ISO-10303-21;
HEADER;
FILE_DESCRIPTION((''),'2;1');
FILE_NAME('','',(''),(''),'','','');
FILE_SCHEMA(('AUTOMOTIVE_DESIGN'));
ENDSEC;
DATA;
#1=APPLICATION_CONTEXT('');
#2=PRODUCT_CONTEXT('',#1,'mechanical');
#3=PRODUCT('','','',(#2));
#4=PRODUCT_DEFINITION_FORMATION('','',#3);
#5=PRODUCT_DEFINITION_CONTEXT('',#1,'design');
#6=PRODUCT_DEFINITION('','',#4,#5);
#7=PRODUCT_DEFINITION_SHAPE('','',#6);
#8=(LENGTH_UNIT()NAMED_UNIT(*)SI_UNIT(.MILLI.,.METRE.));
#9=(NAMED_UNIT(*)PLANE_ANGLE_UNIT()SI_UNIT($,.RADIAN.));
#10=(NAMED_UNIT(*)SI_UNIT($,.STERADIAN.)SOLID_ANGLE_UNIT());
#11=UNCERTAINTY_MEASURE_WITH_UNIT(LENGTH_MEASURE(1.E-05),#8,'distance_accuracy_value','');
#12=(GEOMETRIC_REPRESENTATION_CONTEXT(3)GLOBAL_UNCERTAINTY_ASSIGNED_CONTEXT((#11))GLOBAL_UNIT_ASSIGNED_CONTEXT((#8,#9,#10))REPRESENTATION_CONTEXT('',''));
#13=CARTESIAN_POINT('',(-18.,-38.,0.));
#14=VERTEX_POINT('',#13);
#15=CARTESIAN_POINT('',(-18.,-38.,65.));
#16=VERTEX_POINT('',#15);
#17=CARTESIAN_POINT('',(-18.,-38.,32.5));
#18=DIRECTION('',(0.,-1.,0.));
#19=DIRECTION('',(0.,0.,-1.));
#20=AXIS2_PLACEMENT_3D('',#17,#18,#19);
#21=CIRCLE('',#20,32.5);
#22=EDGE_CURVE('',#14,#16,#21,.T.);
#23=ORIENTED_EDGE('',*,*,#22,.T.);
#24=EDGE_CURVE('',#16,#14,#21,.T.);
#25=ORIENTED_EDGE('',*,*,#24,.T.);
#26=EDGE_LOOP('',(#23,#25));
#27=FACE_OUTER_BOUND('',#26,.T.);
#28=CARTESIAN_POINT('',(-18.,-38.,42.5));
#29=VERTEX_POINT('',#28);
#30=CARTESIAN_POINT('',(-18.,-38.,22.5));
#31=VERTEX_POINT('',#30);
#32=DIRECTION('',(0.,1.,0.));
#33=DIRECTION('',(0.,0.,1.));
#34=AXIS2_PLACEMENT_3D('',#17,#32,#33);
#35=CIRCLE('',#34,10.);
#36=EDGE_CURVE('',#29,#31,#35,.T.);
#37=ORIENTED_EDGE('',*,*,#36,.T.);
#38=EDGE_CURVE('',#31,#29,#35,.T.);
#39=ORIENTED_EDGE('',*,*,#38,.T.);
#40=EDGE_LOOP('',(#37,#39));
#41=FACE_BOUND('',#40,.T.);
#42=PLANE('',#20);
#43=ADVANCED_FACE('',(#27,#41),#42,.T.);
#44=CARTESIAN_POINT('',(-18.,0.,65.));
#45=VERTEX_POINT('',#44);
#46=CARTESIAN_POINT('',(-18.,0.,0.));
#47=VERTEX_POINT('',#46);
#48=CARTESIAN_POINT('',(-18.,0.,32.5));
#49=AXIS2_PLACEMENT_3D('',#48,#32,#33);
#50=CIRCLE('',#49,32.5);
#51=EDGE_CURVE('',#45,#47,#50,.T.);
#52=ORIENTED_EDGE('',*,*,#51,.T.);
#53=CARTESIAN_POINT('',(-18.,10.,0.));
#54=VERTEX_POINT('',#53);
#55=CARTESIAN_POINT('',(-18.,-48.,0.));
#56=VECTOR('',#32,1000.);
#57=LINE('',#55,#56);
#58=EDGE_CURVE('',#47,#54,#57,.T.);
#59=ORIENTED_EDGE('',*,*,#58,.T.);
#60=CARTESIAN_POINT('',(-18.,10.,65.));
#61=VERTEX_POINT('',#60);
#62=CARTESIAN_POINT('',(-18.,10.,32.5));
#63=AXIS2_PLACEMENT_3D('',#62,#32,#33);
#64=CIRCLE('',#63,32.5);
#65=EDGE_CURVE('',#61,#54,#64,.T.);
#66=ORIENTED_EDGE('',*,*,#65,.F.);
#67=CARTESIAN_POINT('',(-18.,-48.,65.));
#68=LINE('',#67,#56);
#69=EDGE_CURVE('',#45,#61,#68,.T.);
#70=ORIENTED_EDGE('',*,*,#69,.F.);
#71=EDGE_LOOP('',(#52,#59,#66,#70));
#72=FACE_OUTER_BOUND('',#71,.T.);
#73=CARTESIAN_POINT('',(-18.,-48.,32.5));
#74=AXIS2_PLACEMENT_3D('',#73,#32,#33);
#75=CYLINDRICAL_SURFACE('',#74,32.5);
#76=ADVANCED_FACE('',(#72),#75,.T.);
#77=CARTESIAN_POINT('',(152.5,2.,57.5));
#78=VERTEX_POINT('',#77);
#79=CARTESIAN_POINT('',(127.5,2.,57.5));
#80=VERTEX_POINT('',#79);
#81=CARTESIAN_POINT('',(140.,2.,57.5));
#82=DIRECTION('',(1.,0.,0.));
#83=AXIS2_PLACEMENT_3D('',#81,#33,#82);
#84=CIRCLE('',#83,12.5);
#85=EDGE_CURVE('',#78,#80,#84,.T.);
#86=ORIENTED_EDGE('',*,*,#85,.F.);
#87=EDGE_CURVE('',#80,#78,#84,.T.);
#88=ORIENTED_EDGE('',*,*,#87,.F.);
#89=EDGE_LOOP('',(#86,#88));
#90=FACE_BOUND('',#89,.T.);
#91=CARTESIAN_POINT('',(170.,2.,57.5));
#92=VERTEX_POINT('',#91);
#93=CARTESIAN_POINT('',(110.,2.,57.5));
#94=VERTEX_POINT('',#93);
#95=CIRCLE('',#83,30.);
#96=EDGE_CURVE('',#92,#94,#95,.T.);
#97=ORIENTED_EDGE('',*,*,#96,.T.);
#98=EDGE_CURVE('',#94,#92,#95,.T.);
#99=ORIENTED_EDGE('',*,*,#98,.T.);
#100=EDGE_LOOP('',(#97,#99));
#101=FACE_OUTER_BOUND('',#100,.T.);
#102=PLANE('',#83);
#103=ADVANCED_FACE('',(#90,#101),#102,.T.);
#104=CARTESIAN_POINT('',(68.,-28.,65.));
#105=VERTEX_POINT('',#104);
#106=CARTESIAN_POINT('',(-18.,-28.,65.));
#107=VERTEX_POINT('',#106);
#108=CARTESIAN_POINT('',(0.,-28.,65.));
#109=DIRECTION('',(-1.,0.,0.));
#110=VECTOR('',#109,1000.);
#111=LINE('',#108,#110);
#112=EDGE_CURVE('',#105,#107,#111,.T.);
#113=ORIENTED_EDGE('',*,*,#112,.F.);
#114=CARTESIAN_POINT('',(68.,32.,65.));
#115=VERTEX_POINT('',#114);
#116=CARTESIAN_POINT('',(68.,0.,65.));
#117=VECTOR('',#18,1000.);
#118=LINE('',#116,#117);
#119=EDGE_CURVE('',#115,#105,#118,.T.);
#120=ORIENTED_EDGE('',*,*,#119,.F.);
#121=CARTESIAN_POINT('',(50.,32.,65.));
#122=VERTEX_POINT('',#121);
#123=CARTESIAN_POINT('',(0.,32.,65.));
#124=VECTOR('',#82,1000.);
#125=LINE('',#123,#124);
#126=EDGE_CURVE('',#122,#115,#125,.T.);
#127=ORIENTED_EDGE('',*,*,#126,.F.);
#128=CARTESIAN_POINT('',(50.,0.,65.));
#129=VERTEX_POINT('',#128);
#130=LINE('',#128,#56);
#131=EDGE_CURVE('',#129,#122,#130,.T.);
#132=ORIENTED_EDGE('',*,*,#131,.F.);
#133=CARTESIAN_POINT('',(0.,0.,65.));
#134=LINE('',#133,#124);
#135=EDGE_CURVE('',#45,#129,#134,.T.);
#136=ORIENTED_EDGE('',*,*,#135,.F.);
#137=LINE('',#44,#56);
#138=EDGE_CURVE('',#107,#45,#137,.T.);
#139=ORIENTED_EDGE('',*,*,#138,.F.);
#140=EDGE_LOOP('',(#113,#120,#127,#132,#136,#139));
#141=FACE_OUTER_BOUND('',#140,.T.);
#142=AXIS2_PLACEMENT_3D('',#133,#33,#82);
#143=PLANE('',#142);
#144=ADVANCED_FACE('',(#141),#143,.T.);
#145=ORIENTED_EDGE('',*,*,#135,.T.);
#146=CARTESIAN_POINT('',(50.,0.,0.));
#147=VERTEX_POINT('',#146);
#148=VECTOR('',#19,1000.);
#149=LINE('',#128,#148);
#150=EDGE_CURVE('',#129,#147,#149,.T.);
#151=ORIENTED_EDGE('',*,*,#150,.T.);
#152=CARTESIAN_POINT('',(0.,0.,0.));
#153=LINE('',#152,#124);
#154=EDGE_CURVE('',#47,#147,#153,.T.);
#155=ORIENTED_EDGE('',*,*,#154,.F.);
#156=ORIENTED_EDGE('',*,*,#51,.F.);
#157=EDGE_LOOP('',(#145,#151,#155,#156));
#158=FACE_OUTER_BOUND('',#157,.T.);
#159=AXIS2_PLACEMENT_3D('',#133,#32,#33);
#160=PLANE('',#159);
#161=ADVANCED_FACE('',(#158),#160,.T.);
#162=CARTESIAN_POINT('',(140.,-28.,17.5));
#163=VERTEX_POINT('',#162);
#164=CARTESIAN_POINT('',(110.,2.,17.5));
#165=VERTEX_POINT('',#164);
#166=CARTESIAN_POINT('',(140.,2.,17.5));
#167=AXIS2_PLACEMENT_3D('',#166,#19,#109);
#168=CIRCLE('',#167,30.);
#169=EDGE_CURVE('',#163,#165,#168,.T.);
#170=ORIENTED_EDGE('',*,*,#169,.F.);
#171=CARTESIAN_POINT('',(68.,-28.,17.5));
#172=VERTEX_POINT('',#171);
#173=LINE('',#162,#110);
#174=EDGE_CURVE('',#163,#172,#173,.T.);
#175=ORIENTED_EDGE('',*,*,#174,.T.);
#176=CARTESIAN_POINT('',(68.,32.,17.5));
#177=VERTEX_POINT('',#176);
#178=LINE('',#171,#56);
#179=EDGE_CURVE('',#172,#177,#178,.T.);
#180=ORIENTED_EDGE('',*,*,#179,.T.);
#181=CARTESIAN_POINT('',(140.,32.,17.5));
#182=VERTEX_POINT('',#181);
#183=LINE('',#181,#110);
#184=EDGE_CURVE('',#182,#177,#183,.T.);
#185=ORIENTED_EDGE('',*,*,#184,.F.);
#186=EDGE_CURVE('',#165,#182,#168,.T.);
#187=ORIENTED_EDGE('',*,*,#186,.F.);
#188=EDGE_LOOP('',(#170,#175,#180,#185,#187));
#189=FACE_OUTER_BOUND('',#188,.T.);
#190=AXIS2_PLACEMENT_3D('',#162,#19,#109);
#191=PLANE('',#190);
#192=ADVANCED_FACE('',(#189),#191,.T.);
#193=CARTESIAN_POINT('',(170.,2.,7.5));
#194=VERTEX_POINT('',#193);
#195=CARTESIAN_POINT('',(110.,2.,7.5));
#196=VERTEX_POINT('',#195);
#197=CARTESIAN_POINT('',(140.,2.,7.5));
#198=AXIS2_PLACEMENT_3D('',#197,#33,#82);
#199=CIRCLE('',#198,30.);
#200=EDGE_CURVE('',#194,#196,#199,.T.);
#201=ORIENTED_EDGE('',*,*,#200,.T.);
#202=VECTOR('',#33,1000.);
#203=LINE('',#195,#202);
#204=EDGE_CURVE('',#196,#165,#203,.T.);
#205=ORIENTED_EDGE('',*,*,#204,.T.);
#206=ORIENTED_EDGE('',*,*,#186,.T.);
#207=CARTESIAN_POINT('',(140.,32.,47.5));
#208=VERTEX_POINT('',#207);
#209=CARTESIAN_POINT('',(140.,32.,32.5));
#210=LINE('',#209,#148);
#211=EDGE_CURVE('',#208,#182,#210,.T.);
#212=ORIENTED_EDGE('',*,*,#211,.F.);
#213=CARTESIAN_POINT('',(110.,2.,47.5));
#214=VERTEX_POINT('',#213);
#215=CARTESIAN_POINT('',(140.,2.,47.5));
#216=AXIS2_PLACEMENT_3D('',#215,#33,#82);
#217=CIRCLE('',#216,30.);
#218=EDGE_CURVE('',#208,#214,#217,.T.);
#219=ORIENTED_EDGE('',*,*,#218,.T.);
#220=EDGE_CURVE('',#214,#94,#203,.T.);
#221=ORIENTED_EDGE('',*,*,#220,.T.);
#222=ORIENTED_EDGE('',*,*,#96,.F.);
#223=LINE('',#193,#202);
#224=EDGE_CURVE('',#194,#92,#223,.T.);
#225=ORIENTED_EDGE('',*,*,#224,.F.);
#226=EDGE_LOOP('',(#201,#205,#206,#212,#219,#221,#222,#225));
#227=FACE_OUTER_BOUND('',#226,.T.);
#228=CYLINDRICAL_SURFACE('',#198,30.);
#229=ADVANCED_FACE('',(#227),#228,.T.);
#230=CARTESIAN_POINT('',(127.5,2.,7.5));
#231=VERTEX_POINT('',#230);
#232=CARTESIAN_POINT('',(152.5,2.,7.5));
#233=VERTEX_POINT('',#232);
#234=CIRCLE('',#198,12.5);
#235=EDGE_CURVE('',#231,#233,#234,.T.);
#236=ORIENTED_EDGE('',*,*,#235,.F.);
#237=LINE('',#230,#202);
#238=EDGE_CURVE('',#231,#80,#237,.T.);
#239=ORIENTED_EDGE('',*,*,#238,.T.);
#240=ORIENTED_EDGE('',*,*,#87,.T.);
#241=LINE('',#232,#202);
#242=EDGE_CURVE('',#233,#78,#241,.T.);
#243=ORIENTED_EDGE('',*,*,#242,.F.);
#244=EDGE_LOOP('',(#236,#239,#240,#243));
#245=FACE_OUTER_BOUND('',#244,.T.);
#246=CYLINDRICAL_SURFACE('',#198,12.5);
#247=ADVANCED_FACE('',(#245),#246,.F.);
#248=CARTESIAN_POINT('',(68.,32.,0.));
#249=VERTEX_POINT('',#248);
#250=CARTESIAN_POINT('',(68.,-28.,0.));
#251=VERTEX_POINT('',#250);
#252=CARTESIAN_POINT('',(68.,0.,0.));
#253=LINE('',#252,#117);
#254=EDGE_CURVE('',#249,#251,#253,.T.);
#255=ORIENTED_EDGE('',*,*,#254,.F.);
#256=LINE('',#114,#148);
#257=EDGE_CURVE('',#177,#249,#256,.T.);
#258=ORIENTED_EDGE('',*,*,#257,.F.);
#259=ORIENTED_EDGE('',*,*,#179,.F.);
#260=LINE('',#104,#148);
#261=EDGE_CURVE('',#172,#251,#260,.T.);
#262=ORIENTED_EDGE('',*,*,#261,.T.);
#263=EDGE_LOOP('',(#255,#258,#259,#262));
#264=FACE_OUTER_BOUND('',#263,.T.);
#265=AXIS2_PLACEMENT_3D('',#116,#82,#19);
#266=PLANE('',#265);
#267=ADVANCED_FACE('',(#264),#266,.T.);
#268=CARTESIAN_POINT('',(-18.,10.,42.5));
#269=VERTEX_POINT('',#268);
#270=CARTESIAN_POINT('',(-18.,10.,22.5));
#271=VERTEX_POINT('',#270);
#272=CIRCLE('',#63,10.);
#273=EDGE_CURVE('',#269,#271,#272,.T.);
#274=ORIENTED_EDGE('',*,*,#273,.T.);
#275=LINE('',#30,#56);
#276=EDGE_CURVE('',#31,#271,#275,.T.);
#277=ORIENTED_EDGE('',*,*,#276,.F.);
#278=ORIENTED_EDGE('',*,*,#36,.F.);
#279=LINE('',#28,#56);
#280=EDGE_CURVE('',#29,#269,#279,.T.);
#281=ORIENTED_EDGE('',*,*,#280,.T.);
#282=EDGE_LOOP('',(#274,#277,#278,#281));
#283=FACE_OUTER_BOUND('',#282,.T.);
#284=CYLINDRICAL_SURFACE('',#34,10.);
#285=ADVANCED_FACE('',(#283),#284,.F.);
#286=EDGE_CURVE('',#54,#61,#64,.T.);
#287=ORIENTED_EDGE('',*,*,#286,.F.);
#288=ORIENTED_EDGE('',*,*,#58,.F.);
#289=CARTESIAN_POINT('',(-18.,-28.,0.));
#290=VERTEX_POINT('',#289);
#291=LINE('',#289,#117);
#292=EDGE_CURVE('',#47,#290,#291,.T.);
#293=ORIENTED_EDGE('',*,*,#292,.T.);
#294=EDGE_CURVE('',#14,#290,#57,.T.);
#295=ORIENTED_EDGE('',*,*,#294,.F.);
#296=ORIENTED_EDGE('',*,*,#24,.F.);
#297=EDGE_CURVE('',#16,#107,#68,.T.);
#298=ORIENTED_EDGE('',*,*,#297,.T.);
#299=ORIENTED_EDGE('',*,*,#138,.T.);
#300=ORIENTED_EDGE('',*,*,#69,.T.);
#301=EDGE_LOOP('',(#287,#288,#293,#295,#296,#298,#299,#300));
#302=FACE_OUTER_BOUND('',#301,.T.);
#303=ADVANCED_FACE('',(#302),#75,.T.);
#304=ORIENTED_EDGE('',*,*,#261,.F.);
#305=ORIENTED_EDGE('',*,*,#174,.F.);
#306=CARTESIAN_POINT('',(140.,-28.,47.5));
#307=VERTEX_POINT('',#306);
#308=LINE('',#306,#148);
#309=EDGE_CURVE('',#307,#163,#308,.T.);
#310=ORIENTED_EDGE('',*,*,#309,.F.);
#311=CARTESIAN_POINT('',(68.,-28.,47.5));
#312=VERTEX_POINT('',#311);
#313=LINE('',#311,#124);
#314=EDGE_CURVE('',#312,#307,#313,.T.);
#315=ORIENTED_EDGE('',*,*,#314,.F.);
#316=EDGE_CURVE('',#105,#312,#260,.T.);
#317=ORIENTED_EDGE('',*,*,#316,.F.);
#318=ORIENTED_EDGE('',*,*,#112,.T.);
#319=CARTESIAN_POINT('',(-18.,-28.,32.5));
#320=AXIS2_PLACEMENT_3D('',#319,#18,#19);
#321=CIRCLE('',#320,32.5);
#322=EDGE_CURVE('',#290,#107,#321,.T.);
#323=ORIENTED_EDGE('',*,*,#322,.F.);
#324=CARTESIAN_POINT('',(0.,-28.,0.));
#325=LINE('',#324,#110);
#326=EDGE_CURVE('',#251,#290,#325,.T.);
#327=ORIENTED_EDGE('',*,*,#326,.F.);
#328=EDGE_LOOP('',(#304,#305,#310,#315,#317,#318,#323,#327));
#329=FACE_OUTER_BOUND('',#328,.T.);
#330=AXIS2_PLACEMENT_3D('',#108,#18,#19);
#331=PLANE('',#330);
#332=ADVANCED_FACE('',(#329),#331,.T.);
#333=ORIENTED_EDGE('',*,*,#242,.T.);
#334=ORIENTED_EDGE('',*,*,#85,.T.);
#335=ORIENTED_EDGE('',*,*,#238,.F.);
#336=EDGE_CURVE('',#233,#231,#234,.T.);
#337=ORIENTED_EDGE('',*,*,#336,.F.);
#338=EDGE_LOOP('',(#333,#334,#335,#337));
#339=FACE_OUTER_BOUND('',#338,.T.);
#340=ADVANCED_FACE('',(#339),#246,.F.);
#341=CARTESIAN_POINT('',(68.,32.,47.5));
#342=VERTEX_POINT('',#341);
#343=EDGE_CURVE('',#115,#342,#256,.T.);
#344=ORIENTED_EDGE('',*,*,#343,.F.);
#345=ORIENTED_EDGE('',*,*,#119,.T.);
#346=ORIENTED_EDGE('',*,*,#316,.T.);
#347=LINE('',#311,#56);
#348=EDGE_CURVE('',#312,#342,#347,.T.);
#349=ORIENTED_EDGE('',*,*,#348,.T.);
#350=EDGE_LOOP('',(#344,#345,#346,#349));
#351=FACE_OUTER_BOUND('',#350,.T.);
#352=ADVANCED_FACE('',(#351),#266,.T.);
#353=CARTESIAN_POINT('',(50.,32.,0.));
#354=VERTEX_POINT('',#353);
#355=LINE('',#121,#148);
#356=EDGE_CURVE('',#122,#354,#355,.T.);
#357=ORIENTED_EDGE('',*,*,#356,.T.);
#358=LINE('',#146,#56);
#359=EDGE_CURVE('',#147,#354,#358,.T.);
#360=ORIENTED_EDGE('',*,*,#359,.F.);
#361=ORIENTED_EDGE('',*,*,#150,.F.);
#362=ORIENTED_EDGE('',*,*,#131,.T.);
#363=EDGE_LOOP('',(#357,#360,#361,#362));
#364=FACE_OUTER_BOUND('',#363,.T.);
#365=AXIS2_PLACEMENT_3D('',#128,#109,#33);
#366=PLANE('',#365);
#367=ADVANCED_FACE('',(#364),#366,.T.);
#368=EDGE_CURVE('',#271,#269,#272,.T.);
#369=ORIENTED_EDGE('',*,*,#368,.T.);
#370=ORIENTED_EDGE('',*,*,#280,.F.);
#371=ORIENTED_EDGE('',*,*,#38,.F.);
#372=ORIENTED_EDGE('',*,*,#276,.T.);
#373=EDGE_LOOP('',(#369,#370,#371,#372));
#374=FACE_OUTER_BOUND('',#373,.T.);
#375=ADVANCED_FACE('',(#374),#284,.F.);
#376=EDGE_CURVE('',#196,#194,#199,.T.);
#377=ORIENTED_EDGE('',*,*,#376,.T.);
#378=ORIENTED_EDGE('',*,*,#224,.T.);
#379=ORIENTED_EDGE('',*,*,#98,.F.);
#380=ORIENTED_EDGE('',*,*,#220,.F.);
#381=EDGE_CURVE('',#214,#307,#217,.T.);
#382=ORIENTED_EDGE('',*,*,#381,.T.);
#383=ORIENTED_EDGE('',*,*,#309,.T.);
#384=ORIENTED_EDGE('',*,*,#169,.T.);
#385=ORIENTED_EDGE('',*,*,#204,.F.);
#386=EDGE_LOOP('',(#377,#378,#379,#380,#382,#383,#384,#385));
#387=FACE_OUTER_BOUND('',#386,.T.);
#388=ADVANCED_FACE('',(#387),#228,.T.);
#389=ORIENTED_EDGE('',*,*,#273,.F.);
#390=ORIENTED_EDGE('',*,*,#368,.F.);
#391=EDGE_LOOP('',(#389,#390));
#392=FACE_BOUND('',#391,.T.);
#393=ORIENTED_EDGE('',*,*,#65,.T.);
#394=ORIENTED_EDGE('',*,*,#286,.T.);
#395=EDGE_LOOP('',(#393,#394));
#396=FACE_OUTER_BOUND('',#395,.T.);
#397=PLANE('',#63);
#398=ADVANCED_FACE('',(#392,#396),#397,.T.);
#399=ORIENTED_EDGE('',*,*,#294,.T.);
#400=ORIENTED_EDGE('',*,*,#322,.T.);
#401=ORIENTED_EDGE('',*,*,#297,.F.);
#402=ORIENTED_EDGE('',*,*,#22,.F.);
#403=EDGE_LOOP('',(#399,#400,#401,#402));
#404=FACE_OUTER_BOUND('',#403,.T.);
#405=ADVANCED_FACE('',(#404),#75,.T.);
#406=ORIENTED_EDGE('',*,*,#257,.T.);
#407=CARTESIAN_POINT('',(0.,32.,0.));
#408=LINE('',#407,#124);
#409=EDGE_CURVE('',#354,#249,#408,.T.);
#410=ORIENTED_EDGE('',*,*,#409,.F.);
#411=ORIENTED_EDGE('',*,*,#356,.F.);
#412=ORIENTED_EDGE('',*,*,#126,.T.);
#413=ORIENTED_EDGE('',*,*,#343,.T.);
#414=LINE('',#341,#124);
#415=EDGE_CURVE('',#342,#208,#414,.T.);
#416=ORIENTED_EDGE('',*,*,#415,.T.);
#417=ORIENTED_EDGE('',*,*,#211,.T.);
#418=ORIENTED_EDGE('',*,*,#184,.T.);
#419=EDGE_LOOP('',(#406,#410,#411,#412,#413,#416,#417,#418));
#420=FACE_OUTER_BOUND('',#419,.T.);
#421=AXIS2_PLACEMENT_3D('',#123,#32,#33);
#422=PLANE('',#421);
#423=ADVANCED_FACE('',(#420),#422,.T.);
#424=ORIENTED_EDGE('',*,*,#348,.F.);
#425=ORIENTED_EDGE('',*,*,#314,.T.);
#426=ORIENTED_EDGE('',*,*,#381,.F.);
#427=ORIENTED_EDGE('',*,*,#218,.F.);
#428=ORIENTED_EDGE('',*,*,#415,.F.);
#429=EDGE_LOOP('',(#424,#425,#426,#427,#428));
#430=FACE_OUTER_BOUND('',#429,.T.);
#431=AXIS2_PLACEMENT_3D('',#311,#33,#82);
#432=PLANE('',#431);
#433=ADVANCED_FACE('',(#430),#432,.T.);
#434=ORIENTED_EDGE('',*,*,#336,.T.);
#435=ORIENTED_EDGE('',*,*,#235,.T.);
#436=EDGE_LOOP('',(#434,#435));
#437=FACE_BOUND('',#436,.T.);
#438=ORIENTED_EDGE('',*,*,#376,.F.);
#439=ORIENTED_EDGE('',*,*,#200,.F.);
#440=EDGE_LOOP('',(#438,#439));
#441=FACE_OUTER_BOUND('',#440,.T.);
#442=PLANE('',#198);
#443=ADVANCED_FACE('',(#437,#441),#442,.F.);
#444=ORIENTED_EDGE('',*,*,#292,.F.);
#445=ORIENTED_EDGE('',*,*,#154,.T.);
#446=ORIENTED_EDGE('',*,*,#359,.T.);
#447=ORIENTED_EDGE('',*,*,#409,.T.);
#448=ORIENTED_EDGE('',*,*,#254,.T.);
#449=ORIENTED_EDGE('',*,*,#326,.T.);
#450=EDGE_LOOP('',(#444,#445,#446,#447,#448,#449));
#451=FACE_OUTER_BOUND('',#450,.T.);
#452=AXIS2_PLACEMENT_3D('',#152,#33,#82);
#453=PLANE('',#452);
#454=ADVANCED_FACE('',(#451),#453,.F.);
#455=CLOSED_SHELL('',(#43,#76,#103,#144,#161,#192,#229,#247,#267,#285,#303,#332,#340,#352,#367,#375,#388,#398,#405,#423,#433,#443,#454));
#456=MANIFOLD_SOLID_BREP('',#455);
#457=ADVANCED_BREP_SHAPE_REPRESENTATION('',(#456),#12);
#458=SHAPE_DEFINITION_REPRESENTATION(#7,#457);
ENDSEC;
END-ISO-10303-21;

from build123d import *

# Parameters (mm, degrees)
MAIN_BODY_DEPTH                 = 65
CENTER_PAD_SKETCH_W             = 65
CENTER_PAD_SKETCH_H             = 28
CENTER_PAD_DEPTH                = 18
VERTICAL_BOSS_SKETCH_R          = 32.5
VERTICAL_BOSS_DEPTH             = 48
VERTICAL_START                  = 10
VERTICAL_BOSS_COLLAR_SKETCH_R   = 32.5
VERTICAL_BOSS_COLLAR_DEPTH      = 10
VERTICAL_START_2                = -10
VERTICAL_BOSS_RELIEF_SKETCH_R   = 32.5
VERTICAL_BOSS_RELIEF_CUT_DEPTH  = 10
VERTICAL_BORE_SKETCH_R          = 10
VERTICAL_BORE_20_DEPTH          = 48
ARM_DEPTH                       = 60
HORIZONTAL_BOSS_SKETCH_R        = 30
HORIZONTAL_BOSS_DEPTH           = 40
HORIZONTAL_START                = 10
HORIZONTAL_BOSS_COLLAR_SKETCH_R = 30
HORIZONTAL_BOSS_COLLAR_DEPTH    = 10
HORIZONTAL_BORE_SKETCH_R        = 12.5
HORIZONTAL_BORE_25_DEPTH        = 50


with BuildPart() as part:
    # Main Body Sketch → Main Body (new body)
    with BuildSketch(Plane.XY):
        Polygon((0, -28), (0, 0), (50, 0), (50, 32), (68, 32), (68, -28), align=None)
    extrude(amount=MAIN_BODY_DEPTH)

    # Center Pad Sketch → Center Pad (add)
    with BuildSketch(Plane.ZY):
        with Locations((32.5, -14)):
            Rectangle(CENTER_PAD_SKETCH_W, CENTER_PAD_SKETCH_H)
    extrude(amount=CENTER_PAD_DEPTH)

    # Vertical Boss Sketch → Vertical Boss (add)
    with BuildSketch(Plane(origin=(0, 0, 0), x_dir=(1, 0, 0), z_dir=(0, 1, 0))):
        with Locations(Location((-18, -32.5, 0), (0, 0, 270))):
            Circle(VERTICAL_BOSS_SKETCH_R)
    extrude(amount=-VERTICAL_BOSS_DEPTH)

    # Vertical Boss Collar Sketch → Vertical Boss Collar (add)
    with BuildSketch(Plane(origin=(0, 0, 0), x_dir=(1, 0, 0), z_dir=(0, 1, 0)).offset(VERTICAL_START)):
        with Locations(Location((-18, -32.5, 0), (0, 0, 270))):
            Circle(VERTICAL_BOSS_COLLAR_SKETCH_R)
    extrude(amount=-VERTICAL_BOSS_COLLAR_DEPTH)

    # Vertical Boss Relief Sketch → Vertical Boss Relief Cut (cut)
    with BuildSketch(Plane.XZ.offset(48).offset(VERTICAL_START_2)):
        with Locations(Location((-18, 32.5, 0), (0, 0, 90))):
            Circle(VERTICAL_BOSS_RELIEF_SKETCH_R)
    extrude(amount=VERTICAL_BOSS_RELIEF_CUT_DEPTH, mode=Mode.SUBTRACT)

    # Vertical Bore Sketch → Vertical Bore Ø20 (cut)
    with BuildSketch(Plane(origin=(0, 10, 0), x_dir=(1, 0, 0), z_dir=(0, 1, 0))):
        with Locations(Location((-18, -32.5, 0), (0, 0, 270))):
            Circle(VERTICAL_BORE_SKETCH_R)
    extrude(amount=-VERTICAL_BORE_20_DEPTH, mode=Mode.SUBTRACT)

    # Arm Sketch → Arm (add)
    with BuildSketch(Plane(origin=(0, 32, 0), x_dir=(1, 0, 0), z_dir=(0, 1, 0))):
        Polygon((140, -32.5), (140, -17.5), (68, -17.5), (68, -47.5), (140, -47.5), align=None)
    extrude(amount=-ARM_DEPTH)

    # Horizontal Boss Sketch → Horizontal Boss (add)
    with BuildSketch(Plane.XY.offset(47.5)):
        with Locations((140, 2)):
            Circle(HORIZONTAL_BOSS_SKETCH_R)
    extrude(amount=-HORIZONTAL_BOSS_DEPTH)

    # Horizontal Boss Collar Sketch → Horizontal Boss Collar (add)
    with BuildSketch(Plane.XY.offset(47.5).offset(HORIZONTAL_START)):
        with Locations((140, 2)):
            Circle(HORIZONTAL_BOSS_COLLAR_SKETCH_R)
    extrude(amount=-HORIZONTAL_BOSS_COLLAR_DEPTH)

    # Horizontal Bore Sketch → Horizontal Bore Ø25 (cut)
    with BuildSketch(Plane.XY.offset(57.5)):
        with Locations((140, 2)):
            Circle(HORIZONTAL_BORE_SKETCH_R)
    extrude(amount=-HORIZONTAL_BORE_25_DEPTH, mode=Mode.SUBTRACT)


solid = part.part
